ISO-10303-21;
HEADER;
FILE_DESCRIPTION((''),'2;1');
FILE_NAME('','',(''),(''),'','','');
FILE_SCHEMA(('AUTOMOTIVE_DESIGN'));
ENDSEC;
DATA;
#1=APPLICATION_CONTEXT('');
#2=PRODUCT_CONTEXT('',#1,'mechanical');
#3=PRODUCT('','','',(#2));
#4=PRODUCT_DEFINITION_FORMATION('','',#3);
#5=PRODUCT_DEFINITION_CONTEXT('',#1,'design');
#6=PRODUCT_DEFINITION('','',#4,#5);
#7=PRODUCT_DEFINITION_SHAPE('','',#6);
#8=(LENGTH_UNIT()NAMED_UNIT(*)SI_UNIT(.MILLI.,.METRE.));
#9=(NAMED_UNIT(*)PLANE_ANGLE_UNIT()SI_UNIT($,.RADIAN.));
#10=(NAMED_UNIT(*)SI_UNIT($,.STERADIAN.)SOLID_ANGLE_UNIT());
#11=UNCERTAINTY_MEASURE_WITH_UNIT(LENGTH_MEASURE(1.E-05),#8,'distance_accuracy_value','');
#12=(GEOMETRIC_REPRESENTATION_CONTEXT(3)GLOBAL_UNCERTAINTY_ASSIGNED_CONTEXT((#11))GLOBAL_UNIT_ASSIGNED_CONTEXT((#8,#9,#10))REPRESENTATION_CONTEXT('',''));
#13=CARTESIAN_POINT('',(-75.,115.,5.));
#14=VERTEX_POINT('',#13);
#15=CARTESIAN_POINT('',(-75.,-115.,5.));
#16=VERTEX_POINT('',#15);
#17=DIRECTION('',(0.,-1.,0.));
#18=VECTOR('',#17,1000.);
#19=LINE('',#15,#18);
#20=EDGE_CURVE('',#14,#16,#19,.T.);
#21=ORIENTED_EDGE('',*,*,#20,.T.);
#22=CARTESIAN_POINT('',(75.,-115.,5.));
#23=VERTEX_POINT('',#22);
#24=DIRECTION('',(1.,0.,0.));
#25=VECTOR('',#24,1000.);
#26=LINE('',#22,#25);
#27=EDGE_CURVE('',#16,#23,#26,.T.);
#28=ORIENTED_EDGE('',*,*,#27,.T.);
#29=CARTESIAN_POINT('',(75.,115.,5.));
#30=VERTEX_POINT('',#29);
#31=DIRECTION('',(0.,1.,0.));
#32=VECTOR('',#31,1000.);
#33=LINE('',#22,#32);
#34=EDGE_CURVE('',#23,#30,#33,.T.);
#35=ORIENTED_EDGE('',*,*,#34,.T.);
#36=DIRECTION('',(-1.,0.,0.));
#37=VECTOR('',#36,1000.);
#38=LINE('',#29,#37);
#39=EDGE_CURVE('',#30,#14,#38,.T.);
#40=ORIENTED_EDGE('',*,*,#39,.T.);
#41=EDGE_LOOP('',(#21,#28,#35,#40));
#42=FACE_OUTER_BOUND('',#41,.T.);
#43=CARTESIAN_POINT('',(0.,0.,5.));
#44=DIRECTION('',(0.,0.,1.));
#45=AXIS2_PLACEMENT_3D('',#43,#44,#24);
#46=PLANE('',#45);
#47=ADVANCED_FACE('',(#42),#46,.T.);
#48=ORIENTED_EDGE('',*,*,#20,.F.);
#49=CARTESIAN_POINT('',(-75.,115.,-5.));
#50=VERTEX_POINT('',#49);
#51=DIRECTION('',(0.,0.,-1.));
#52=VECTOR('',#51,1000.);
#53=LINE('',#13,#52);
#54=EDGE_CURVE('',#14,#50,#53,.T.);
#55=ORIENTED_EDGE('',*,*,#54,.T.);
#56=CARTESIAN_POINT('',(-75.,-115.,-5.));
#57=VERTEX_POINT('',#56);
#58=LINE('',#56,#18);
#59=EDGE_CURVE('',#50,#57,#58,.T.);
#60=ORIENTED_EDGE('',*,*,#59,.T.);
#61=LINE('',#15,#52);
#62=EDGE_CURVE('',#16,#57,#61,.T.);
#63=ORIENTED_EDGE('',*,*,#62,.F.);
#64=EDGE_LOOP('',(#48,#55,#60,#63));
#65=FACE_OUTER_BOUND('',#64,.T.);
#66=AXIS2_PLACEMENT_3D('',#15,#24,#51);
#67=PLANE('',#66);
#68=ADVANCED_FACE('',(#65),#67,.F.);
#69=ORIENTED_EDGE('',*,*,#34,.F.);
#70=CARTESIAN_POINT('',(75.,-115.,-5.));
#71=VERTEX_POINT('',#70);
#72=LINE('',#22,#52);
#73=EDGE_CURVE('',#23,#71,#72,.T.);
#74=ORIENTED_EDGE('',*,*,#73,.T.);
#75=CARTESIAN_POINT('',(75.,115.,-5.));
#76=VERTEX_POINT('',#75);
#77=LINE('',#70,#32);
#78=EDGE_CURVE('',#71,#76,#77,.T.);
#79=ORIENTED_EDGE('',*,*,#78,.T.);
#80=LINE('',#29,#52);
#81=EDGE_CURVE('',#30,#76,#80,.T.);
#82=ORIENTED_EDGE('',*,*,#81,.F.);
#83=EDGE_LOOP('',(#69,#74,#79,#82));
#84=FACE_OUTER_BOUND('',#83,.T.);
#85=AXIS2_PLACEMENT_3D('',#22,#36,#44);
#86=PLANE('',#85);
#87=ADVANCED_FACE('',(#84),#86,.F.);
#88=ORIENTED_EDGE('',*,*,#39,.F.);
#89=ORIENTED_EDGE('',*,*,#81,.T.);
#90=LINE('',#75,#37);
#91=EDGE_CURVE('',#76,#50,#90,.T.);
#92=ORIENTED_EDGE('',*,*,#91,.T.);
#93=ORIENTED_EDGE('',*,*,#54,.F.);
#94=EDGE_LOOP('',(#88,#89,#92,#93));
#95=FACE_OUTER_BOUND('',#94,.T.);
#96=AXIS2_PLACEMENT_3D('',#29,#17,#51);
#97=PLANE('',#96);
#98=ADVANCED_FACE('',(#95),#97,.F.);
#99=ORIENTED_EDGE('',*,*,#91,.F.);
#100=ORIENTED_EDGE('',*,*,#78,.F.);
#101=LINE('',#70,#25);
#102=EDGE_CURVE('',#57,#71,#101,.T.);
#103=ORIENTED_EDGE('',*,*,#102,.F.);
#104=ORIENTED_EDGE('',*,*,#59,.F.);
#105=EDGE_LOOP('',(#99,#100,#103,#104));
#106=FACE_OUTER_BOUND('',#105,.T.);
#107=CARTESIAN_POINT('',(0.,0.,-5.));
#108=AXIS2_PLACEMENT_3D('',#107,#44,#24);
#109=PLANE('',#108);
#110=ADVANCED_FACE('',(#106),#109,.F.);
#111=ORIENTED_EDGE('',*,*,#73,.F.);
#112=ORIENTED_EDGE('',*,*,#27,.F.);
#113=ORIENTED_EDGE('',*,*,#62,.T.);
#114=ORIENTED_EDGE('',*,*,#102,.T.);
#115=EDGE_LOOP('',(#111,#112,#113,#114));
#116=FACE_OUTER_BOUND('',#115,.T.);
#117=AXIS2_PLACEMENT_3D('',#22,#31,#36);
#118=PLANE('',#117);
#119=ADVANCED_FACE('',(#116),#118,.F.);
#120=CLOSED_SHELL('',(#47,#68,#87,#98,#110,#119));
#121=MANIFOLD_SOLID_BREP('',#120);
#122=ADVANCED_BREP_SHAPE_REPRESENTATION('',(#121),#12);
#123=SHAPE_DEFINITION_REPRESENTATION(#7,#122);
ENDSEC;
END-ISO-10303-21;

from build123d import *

# Parameters (mm, degrees)
SKETCH1_W           = 150
SKETCH1_H           = 230
BOSS_EXTRUDE1_DEPTH = 5


with BuildPart() as part:
    # Sketch1 → Boss-Extrude1 (new, symmetric)
    with BuildSketch(Plane.XY):
        Rectangle(SKETCH1_W, SKETCH1_H)
    extrude(amount=BOSS_EXTRUDE1_DEPTH, both=True)


solid = part.part
